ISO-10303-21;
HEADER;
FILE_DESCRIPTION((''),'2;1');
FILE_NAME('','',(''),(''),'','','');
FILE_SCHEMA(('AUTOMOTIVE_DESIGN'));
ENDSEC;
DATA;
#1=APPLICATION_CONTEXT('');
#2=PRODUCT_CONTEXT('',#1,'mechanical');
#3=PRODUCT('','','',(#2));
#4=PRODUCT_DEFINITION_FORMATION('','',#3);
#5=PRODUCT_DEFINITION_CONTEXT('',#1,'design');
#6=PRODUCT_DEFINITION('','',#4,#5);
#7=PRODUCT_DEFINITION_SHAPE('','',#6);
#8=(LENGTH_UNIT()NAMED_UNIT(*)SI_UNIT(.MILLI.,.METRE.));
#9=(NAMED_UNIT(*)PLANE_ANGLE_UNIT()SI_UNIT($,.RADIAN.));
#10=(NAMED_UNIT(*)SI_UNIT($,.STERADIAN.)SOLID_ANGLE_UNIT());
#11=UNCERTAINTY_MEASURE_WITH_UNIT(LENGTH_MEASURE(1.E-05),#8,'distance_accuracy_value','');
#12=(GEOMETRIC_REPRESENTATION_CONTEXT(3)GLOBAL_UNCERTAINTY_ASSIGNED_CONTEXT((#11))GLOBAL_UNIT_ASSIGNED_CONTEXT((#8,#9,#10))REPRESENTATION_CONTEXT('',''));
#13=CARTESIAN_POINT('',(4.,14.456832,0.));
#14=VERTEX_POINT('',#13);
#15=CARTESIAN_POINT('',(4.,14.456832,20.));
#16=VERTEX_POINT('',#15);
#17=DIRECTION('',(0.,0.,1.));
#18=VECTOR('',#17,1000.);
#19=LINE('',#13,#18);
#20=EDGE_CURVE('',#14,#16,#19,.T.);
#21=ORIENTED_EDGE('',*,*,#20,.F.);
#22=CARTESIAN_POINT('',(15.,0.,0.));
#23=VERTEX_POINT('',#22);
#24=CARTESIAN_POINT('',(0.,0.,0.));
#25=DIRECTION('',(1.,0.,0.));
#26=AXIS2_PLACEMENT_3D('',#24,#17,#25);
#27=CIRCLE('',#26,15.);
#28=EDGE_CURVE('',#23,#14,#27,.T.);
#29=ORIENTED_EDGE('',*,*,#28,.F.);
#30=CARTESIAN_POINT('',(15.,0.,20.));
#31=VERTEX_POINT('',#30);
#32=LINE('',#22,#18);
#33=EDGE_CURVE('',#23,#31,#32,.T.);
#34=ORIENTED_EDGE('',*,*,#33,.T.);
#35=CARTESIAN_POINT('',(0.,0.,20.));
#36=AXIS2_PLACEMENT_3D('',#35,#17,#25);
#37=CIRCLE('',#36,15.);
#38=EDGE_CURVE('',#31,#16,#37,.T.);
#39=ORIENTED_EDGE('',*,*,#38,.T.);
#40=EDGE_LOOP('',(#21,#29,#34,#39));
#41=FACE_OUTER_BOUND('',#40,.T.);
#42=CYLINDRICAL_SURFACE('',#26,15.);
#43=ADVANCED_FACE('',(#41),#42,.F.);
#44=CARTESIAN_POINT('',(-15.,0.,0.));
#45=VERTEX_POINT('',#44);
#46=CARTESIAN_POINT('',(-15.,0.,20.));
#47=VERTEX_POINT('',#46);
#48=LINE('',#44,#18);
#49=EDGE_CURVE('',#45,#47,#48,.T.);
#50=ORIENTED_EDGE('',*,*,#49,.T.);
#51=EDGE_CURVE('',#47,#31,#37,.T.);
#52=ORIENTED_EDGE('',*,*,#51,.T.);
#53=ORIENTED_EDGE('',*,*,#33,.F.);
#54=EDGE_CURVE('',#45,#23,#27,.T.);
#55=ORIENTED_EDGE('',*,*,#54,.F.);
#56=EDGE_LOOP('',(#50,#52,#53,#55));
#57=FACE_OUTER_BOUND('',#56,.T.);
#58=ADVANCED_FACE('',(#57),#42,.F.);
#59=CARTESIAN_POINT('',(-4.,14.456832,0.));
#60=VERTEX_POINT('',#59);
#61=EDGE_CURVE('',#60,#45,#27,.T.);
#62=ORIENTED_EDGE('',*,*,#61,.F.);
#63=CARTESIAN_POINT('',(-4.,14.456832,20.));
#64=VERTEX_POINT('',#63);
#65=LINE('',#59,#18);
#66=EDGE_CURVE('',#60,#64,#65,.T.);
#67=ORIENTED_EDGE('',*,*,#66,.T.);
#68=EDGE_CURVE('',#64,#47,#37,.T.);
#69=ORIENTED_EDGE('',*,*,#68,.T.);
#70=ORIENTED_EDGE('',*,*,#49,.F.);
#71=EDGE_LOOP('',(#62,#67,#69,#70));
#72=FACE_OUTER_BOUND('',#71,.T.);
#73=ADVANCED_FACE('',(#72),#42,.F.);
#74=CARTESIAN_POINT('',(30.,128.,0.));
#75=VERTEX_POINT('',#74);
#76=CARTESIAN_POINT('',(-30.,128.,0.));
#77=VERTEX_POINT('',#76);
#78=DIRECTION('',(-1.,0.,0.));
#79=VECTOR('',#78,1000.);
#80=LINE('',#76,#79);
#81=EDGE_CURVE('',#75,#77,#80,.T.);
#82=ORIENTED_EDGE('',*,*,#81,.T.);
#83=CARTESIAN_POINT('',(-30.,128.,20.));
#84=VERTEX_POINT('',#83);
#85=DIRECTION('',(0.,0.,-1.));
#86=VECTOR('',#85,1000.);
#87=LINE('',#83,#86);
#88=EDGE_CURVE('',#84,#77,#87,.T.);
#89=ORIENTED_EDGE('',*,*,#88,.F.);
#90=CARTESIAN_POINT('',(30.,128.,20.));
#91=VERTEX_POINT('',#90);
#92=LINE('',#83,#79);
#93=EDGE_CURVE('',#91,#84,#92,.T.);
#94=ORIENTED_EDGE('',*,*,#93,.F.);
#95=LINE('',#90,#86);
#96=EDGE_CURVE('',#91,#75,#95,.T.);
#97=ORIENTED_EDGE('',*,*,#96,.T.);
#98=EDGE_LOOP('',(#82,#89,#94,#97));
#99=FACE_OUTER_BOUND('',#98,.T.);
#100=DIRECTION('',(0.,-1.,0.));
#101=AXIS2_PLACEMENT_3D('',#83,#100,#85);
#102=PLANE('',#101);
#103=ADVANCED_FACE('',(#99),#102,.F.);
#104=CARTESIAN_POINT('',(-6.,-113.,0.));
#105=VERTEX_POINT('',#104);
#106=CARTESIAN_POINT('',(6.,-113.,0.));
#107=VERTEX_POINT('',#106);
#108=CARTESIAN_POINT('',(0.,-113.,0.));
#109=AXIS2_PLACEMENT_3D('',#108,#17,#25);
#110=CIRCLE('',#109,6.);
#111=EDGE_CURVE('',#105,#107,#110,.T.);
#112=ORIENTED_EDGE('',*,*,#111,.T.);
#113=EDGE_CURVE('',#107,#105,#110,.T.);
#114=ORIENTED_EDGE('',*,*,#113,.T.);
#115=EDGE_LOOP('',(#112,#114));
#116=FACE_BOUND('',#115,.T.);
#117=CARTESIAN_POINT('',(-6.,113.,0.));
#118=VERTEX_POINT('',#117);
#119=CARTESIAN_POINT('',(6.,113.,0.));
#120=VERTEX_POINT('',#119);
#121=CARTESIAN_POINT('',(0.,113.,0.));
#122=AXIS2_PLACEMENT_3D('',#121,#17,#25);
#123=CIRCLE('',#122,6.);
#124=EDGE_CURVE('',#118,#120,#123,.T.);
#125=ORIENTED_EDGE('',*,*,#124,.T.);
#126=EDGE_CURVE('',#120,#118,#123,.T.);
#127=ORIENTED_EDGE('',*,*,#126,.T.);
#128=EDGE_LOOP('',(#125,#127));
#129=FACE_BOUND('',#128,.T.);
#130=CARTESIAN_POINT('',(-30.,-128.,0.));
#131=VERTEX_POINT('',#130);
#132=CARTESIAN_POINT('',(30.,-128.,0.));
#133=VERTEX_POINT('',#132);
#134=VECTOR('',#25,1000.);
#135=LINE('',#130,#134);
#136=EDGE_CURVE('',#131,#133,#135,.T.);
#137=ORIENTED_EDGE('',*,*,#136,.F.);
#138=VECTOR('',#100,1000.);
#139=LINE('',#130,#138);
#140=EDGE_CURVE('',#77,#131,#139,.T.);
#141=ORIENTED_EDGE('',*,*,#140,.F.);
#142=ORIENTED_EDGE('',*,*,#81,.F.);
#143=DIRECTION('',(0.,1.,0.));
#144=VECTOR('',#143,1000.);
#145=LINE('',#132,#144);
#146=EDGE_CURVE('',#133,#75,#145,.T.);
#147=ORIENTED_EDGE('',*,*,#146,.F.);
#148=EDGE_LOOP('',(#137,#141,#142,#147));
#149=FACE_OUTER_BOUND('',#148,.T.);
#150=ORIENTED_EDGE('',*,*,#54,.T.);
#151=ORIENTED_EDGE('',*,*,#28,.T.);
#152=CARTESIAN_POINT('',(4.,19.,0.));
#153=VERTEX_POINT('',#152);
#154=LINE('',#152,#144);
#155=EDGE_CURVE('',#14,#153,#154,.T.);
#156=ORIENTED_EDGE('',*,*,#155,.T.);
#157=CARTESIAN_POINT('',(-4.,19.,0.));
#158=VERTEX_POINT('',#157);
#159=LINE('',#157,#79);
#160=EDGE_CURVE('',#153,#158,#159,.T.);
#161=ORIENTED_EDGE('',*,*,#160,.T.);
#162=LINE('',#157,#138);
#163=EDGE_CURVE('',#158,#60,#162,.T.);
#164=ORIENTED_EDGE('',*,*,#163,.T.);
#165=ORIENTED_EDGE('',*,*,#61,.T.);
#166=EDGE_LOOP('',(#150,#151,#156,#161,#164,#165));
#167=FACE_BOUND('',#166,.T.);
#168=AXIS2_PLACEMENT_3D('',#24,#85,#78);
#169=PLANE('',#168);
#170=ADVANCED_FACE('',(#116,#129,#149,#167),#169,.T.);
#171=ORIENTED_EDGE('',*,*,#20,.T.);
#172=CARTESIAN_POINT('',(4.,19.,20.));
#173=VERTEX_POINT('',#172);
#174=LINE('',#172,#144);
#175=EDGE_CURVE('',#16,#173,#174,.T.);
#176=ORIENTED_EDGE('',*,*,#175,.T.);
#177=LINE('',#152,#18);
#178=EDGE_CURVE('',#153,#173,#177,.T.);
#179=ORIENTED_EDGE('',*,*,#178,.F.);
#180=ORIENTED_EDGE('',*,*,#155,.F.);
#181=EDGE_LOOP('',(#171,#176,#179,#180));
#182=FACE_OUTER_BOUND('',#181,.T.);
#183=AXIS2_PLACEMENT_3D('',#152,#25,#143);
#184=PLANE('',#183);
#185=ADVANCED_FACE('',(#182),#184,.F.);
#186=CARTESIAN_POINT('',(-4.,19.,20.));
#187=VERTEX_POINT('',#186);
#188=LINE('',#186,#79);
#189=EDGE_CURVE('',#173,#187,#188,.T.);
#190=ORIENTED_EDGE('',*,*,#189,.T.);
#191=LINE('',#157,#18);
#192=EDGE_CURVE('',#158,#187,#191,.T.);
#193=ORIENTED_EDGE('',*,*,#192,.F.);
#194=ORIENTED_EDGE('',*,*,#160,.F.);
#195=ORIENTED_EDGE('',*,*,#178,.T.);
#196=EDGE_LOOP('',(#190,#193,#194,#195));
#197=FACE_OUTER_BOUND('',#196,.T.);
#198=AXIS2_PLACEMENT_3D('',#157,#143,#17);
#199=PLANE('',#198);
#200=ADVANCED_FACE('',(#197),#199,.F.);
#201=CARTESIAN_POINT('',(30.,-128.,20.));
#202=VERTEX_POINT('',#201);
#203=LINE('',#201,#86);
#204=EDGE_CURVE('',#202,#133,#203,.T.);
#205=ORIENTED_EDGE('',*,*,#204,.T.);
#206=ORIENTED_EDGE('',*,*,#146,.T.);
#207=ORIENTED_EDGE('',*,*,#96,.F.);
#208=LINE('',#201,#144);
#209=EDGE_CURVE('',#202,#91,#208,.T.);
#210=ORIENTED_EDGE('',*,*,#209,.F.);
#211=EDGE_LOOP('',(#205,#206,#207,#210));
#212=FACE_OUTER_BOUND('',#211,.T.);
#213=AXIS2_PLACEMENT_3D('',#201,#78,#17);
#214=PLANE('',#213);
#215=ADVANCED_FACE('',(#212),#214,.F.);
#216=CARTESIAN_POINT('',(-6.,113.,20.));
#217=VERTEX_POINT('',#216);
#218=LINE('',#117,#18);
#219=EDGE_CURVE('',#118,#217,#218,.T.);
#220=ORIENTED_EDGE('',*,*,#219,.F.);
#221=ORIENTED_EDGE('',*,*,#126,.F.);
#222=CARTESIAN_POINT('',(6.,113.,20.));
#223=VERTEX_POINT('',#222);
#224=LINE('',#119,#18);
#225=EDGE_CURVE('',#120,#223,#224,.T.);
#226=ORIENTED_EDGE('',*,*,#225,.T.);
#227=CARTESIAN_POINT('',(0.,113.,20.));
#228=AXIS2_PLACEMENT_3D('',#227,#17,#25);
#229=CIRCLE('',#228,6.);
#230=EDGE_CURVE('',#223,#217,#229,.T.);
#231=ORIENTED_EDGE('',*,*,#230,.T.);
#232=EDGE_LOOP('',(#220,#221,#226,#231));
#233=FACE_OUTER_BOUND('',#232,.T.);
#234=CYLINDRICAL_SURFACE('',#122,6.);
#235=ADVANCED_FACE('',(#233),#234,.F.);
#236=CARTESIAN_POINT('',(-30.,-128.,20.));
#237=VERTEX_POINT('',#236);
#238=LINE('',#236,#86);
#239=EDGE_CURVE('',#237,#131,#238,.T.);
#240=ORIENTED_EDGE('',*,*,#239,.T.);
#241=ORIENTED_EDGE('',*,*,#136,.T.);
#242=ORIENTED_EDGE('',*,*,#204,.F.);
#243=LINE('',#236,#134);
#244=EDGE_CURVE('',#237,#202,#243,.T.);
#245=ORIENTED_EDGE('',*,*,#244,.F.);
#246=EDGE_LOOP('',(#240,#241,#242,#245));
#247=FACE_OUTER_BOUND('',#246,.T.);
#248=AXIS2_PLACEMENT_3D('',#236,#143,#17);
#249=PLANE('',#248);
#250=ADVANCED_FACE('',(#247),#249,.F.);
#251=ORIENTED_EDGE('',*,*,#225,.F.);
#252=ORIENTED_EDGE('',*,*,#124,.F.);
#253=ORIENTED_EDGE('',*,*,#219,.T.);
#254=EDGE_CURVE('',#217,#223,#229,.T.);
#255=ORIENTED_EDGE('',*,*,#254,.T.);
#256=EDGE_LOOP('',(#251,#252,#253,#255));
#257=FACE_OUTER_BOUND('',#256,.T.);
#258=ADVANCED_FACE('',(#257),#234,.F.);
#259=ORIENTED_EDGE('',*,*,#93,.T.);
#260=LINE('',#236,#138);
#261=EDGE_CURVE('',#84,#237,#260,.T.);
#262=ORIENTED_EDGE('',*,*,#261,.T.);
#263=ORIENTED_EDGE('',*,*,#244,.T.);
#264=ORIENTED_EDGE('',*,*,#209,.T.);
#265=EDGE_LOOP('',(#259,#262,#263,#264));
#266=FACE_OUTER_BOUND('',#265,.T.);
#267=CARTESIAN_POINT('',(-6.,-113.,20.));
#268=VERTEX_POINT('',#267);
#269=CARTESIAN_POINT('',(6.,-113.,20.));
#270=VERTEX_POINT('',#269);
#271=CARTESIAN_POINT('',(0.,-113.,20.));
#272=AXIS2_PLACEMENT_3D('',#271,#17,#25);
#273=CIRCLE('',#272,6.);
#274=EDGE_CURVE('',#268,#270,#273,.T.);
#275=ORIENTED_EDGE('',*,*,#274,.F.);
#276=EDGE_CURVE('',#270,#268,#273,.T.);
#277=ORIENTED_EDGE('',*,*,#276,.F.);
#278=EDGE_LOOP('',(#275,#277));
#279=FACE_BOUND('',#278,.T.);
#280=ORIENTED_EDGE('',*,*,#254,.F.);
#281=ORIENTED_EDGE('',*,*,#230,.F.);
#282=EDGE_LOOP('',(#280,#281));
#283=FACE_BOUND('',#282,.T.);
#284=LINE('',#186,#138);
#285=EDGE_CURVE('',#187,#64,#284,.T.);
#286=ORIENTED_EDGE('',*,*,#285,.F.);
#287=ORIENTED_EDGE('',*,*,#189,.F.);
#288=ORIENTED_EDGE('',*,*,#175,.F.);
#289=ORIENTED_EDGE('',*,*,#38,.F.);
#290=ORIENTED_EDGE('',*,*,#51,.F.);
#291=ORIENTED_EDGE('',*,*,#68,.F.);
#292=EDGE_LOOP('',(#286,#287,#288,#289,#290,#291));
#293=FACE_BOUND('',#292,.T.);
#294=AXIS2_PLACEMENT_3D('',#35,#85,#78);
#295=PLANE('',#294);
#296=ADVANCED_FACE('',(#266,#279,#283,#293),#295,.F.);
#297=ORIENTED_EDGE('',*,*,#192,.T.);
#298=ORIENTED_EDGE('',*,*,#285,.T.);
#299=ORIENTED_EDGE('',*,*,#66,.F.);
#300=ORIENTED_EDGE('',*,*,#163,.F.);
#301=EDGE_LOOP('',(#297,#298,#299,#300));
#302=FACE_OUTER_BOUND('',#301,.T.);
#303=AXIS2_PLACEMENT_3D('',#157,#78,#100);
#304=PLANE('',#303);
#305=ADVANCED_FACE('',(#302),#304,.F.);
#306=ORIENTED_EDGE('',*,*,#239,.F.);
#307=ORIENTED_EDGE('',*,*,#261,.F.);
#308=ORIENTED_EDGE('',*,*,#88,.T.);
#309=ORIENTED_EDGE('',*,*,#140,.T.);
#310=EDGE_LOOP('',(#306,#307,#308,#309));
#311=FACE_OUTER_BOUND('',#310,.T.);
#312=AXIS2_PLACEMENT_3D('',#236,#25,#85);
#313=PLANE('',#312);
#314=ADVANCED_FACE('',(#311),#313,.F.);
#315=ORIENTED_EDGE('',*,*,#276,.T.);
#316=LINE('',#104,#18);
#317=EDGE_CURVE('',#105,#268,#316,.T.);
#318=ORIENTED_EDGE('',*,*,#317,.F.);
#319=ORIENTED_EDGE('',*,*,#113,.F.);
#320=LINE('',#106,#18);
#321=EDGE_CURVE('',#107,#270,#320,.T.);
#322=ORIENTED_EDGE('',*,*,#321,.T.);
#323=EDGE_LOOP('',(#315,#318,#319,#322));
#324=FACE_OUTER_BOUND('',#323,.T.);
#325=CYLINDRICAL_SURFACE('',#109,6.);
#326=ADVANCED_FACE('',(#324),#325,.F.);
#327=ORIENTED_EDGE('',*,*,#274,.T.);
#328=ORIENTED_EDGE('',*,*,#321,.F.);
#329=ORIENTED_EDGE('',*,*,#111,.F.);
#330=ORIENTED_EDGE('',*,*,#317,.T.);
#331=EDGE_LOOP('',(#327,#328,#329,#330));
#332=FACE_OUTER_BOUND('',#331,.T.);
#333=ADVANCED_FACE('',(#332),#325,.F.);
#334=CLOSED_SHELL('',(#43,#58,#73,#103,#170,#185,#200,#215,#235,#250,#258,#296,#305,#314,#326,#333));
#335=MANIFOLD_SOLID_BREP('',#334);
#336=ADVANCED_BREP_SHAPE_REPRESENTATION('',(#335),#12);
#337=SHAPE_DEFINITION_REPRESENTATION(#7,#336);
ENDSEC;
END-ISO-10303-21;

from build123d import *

# Parameters (mm, degrees)
SKETCH_1_W          = 60
SKETCH_1_H          = 256
EXTRUDE_1_DEPTH     = 20
SKETCH_2_R          = 6
CUT_EXTRUDE_1_DEPTH = 133.981201679
CUT_EXTRUDE_2_DEPTH = 133.981201679


with BuildPart() as part:
    # 草图1 → 凸台-拉伸1 (new body)
    with BuildSketch(Plane.XY):
        Rectangle(SKETCH_1_W, SKETCH_1_H)
    extrude(amount=EXTRUDE_1_DEPTH)

    # 草图2 → 切除-拉伸1 (cut, through all)
    with BuildSketch(Plane.XY.offset(20)):
        with Locations((0, 113)):
            Circle(SKETCH_2_R)
        with Locations((0, -113)):
            Circle(SKETCH_2_R)
    extrude(amount=-CUT_EXTRUDE_1_DEPTH, mode=Mode.SUBTRACT)

    # 草图3 → 切除-拉伸2 (cut, through all)
    with BuildSketch(Plane.XY.offset(20)):
        with BuildLine():
            Line((-4, 19), (4, 19))
            Line((4, 19), (4, 14.456832295))
            ThreePointArc((4, 14.456832295), (0, -15), (-4, 14.456832295))
            Line((-4, 14.456832295), (-4, 19))
        make_face()
    extrude(amount=-CUT_EXTRUDE_2_DEPTH, mode=Mode.SUBTRACT)


solid = part.part
